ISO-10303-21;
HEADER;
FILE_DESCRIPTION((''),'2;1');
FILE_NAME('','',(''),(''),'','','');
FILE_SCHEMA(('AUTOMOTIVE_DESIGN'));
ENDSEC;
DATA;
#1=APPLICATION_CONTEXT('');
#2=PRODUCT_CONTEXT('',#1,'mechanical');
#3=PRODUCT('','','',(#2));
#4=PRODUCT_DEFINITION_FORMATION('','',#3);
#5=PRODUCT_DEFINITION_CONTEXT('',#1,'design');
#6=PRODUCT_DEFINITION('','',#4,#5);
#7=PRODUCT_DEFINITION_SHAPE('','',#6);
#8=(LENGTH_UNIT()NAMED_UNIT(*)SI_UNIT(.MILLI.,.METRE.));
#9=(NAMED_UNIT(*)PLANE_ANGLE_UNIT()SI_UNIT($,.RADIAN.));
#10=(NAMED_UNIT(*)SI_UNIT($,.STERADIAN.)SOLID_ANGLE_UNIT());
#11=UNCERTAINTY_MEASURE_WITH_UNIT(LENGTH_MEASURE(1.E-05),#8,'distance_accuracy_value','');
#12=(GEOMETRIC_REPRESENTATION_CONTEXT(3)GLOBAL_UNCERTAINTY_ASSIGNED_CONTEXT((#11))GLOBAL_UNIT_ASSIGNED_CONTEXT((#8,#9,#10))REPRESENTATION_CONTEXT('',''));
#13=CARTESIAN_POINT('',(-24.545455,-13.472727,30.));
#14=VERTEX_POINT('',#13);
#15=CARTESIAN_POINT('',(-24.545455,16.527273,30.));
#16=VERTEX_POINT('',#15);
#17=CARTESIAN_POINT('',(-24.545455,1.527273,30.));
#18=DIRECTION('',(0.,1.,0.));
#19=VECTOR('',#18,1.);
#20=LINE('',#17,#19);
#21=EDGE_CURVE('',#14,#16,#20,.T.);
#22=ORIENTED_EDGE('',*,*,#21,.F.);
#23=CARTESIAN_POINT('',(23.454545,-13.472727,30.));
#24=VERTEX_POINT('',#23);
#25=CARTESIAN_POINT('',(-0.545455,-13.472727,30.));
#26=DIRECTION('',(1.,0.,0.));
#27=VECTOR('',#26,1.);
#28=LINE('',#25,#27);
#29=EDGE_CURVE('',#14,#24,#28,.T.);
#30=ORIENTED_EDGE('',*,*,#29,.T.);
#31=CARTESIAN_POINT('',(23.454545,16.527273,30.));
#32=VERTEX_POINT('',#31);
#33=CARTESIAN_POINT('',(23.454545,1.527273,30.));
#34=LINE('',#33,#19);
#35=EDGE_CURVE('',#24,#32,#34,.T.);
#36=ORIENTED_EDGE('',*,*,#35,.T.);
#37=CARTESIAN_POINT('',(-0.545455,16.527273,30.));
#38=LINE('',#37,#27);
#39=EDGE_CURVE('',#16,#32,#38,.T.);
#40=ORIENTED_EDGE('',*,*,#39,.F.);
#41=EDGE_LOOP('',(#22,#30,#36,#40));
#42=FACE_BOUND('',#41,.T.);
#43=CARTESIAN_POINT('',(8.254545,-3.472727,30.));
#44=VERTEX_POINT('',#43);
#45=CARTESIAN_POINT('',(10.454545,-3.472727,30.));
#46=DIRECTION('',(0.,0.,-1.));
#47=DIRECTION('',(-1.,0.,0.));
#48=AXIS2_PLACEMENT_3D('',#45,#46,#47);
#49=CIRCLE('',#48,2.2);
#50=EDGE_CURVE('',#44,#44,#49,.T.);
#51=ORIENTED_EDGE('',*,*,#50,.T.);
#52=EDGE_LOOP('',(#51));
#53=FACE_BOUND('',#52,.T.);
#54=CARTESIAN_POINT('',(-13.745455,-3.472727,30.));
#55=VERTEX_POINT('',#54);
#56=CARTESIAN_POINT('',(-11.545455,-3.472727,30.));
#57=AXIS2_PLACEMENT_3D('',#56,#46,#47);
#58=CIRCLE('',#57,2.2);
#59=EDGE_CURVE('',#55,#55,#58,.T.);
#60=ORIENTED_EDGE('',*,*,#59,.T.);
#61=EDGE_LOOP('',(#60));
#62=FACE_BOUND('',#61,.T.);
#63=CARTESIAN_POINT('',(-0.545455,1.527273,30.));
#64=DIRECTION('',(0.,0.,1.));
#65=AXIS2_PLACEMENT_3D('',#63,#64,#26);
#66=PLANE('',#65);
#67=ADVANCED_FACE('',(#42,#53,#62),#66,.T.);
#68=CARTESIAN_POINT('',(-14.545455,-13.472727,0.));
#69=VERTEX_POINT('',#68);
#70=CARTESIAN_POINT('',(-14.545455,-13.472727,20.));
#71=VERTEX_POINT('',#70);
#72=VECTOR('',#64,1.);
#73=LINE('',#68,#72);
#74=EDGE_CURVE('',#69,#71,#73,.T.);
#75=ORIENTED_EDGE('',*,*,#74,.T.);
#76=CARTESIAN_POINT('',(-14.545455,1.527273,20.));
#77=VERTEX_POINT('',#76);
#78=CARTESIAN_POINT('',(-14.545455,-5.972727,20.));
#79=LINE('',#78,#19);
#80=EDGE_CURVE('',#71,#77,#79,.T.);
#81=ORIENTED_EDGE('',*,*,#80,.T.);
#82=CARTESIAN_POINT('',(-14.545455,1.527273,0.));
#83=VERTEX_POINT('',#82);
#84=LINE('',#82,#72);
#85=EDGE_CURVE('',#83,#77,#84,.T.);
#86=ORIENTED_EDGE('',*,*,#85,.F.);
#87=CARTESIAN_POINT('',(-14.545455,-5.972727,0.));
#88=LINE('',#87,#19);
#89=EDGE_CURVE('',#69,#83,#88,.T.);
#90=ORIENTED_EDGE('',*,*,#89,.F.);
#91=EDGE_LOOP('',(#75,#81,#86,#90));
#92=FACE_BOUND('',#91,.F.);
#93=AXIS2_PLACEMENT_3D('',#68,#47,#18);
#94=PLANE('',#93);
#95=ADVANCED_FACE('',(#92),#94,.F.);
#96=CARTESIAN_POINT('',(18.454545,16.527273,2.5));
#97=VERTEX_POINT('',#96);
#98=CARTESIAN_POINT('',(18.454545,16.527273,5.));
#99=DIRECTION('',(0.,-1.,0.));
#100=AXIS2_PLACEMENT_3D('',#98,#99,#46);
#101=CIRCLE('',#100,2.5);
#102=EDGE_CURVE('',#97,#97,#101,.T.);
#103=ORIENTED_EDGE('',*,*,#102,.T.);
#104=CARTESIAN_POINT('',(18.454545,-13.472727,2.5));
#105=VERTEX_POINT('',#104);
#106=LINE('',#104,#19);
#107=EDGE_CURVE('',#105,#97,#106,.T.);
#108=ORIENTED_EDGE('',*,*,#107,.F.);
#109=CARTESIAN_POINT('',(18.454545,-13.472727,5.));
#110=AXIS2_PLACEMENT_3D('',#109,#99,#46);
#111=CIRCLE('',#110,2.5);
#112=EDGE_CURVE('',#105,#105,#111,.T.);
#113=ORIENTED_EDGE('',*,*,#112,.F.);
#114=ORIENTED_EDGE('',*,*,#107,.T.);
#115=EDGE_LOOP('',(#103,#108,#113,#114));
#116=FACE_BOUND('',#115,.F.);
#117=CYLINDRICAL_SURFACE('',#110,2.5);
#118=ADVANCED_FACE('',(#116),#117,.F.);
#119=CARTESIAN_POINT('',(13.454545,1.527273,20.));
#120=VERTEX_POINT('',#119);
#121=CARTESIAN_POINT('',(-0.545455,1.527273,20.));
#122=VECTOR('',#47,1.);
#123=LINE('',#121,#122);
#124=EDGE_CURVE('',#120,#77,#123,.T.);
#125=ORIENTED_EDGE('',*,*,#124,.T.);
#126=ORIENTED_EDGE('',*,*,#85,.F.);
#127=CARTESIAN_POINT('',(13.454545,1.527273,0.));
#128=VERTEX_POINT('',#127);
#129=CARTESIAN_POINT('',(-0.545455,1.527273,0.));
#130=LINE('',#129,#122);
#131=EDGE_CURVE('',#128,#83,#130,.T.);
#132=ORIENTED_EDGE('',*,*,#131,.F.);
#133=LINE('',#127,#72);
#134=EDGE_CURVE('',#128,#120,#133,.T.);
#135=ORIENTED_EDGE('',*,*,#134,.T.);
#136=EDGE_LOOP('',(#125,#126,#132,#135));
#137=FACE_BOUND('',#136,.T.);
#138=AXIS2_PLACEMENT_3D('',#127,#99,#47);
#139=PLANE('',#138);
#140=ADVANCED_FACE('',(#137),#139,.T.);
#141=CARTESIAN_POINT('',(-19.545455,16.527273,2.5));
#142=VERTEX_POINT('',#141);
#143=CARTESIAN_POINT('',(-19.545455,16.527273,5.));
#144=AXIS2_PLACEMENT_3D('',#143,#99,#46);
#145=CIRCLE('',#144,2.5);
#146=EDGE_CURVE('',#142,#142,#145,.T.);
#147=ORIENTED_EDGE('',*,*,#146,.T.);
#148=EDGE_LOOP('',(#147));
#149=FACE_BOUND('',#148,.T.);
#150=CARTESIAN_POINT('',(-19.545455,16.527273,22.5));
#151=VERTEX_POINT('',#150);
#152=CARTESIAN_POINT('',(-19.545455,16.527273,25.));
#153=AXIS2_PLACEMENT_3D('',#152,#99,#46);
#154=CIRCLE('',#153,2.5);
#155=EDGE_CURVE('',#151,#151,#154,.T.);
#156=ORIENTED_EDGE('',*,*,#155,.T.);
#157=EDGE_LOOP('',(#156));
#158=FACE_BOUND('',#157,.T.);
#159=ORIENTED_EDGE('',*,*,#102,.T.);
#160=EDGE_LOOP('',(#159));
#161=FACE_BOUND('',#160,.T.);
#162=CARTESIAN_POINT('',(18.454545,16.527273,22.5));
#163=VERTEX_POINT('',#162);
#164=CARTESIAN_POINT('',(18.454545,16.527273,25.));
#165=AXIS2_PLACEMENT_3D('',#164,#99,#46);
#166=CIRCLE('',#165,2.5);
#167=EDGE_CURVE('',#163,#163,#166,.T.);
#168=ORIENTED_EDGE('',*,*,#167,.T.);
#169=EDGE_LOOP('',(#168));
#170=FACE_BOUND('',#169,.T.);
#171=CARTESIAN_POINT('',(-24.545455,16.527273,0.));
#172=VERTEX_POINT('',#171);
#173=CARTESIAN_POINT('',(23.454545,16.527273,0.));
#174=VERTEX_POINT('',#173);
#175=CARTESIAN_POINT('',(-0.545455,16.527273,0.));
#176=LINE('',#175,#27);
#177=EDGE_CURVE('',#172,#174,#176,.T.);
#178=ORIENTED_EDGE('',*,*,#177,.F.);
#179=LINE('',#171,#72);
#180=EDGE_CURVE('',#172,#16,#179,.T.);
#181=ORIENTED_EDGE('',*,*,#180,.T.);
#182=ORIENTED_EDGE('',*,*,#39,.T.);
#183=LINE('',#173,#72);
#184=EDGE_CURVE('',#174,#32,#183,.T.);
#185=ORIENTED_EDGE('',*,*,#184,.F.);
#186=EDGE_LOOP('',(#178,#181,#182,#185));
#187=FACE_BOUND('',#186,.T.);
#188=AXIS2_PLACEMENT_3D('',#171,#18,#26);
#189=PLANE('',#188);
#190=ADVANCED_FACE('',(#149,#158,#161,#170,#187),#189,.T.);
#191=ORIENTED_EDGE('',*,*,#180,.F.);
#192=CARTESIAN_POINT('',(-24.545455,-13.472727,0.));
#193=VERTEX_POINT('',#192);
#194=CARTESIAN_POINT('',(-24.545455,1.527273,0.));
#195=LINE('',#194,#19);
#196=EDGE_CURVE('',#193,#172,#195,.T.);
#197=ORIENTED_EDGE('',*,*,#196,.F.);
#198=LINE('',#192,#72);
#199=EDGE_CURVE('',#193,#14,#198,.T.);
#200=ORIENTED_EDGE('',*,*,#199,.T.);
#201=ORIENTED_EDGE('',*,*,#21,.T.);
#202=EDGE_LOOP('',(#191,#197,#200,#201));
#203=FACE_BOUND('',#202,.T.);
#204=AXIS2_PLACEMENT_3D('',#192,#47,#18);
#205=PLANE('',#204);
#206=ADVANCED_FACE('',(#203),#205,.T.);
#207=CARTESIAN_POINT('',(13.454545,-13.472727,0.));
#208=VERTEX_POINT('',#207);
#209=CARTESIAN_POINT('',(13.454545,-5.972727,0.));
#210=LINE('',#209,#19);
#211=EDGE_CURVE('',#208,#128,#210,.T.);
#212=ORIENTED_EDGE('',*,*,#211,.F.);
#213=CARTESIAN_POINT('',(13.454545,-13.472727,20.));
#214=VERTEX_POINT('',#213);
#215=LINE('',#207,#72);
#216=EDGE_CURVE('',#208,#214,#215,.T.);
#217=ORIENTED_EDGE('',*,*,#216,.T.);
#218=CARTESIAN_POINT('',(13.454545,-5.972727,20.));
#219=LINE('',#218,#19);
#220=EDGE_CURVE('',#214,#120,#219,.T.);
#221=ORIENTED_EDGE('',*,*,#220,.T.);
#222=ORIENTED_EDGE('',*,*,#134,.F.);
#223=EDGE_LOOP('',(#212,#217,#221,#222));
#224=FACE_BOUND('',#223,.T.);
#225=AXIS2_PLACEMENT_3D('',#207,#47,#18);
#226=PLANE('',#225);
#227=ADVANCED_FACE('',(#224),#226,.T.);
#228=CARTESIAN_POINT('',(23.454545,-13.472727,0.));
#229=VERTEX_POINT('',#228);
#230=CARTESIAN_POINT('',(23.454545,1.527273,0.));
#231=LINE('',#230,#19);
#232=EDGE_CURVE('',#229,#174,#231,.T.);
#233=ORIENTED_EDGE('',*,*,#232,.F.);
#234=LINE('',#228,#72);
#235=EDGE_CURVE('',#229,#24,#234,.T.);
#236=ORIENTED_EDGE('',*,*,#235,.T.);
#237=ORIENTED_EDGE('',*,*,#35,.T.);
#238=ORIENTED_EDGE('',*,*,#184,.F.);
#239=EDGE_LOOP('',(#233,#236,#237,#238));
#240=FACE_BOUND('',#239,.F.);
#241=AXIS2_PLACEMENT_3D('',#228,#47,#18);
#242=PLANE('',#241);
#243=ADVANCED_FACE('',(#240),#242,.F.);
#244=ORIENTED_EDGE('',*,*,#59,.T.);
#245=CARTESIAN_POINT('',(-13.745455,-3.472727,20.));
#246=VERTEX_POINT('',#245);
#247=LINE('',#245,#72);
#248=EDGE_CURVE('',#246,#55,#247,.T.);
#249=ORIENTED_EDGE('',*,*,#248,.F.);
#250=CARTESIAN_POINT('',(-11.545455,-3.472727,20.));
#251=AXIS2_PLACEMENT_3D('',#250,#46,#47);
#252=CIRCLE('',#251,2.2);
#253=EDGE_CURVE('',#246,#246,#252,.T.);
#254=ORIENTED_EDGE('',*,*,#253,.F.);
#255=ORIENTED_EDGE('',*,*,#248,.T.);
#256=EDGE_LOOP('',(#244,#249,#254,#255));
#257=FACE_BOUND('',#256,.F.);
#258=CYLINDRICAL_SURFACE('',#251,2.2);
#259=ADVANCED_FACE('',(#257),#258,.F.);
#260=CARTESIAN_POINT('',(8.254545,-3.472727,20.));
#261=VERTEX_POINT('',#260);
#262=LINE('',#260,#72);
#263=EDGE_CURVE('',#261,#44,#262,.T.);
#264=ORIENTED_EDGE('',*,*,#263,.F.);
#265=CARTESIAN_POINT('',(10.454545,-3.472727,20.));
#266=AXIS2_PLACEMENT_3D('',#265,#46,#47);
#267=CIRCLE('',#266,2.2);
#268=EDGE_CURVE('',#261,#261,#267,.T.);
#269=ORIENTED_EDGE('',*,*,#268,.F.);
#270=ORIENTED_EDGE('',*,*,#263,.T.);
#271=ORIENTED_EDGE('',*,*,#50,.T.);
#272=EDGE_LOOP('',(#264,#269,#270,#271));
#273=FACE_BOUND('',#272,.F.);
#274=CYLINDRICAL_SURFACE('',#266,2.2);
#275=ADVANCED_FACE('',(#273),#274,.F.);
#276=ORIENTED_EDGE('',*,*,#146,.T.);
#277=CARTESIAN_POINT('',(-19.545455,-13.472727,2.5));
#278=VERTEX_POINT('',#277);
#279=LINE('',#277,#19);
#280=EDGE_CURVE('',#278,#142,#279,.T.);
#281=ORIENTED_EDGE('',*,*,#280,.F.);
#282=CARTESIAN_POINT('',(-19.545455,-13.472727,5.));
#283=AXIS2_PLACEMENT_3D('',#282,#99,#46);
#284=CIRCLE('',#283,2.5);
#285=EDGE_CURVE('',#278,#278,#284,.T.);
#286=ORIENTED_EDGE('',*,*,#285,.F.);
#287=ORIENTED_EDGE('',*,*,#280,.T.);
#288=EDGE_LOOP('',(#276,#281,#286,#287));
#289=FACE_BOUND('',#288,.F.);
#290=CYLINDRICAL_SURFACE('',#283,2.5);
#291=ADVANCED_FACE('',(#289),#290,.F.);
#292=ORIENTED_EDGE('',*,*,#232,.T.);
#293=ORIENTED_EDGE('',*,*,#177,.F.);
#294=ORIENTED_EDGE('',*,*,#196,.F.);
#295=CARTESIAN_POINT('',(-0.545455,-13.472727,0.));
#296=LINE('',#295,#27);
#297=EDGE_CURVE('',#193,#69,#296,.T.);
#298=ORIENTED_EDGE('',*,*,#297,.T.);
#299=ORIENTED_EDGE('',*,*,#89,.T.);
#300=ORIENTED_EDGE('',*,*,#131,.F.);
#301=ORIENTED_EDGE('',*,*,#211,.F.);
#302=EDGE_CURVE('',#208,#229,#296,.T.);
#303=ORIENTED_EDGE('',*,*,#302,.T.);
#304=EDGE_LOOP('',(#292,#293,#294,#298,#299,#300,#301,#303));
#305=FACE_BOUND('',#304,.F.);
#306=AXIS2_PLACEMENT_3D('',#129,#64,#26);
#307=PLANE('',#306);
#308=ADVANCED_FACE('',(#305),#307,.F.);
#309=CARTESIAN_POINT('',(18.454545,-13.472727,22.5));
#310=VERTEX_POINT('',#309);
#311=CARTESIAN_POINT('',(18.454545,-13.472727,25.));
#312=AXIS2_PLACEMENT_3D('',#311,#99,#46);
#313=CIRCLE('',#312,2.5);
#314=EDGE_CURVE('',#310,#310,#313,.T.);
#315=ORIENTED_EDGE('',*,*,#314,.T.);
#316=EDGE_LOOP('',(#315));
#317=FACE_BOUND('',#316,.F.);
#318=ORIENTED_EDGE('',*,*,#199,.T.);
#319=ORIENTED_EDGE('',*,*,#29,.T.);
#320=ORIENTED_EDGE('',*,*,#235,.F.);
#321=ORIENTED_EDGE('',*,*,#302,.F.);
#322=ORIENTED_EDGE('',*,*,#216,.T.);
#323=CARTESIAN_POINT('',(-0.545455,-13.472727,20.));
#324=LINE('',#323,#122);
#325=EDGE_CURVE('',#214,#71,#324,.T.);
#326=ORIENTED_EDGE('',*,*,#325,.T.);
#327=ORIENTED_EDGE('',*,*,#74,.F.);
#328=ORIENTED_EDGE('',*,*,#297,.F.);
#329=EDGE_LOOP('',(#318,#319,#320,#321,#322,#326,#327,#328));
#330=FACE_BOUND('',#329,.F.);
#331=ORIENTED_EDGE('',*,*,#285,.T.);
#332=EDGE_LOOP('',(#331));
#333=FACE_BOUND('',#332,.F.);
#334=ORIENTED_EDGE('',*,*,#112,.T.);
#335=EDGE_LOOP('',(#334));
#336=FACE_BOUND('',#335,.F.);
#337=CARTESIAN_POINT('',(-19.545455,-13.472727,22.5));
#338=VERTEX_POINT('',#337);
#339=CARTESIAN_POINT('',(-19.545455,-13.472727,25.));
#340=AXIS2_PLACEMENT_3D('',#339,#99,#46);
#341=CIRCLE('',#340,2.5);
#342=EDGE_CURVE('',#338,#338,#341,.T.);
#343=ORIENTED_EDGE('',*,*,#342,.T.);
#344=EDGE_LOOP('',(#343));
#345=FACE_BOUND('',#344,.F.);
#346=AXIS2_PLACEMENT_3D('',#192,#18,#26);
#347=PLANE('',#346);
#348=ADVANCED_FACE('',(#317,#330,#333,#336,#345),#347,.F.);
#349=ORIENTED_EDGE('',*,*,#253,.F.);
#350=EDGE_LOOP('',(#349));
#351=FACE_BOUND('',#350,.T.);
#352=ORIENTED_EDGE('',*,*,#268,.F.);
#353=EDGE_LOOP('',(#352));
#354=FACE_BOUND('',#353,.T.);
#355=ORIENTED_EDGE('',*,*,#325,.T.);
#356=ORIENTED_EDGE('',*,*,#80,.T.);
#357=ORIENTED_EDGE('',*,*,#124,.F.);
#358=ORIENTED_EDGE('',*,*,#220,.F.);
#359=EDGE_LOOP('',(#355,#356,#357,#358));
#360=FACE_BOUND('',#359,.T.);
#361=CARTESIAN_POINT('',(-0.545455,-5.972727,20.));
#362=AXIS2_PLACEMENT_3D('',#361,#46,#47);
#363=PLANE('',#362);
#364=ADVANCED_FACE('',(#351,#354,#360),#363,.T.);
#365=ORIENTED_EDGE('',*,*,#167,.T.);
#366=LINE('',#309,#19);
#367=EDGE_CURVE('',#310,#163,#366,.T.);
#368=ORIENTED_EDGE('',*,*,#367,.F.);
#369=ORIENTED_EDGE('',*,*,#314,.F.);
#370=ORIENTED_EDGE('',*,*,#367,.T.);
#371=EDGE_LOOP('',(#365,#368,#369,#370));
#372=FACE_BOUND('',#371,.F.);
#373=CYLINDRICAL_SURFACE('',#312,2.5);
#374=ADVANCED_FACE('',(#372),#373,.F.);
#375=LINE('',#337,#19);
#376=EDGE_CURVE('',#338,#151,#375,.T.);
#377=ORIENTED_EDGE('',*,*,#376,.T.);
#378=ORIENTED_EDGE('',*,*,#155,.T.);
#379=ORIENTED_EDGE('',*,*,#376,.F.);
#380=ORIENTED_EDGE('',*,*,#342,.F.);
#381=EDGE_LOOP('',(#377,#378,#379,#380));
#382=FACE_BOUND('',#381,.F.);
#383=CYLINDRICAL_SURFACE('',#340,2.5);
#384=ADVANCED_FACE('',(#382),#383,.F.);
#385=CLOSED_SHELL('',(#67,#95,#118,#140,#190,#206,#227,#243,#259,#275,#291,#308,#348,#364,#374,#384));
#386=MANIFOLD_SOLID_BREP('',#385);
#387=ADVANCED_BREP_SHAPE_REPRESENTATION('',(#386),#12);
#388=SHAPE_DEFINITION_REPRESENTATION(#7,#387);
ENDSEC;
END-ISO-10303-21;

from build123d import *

# Parameters (mm, degrees)
SKETCH_1_W          = 48
SKETCH_1_H          = 30
EXTRUDE_1_DEPTH     = 30
SKETCH_2_W          = 28
SKETCH_2_H          = 15
CUT_EXTRUDE_1_DEPTH = 20
SKETCH_3_R          = 2.2
CUT_EXTRUDE_2_DEPTH = 20
SKETCH_4_R          = 2.5
CUT_EXTRUDE_3_DEPTH = 30


with BuildPart() as part:
    # 草图1 → 凸台-拉伸1 (new body)
    with BuildSketch(Plane.XY):
        with Locations((-0.545454545, 1.527272727)):
            Rectangle(SKETCH_1_W, SKETCH_1_H)
    extrude(amount=EXTRUDE_1_DEPTH)

    # 草图2 → 切除-拉伸1 (cut)
    with BuildSketch(Plane(origin=(0, 0, 0), x_dir=(-1, 0, 0), z_dir=(0, 0, -1))):
        with Locations((0.545454545, -5.972727273)):
            Rectangle(SKETCH_2_W, SKETCH_2_H)
    extrude(amount=-CUT_EXTRUDE_1_DEPTH, mode=Mode.SUBTRACT)

    # 草图3 → 切除-拉伸2 (cut)
    with BuildSketch(Plane(origin=(0, 0, 20), x_dir=(-1, 0, 0), z_dir=(0, 0, -1))):
        with Locations((-10.454545455, -3.472727273)):
            Circle(SKETCH_3_R)
        with Locations((11.545454545, -3.472727273)):
            Circle(SKETCH_3_R)
    extrude(amount=-CUT_EXTRUDE_2_DEPTH, mode=Mode.SUBTRACT)

    # 草图4 → 切除-拉伸3 (cut)
    with BuildSketch(Plane.XZ.offset(13.472727273)):
        with Locations(Location((-19.545454545, 5, 0), (0, 0, 270))):
            Circle(SKETCH_4_R)
        with Locations(Location((-19.545454545, 25, 0), (0, 0, 270))):
            Circle(SKETCH_4_R)
        with Locations(Location((18.454545455, 25, 0), (0, 0, 270))):
            Circle(SKETCH_4_R)
        with Locations(Location((18.454545455, 5, 0), (0, 0, 270))):
            Circle(SKETCH_4_R)
    extrude(amount=-CUT_EXTRUDE_3_DEPTH, mode=Mode.SUBTRACT)


solid = part.part
